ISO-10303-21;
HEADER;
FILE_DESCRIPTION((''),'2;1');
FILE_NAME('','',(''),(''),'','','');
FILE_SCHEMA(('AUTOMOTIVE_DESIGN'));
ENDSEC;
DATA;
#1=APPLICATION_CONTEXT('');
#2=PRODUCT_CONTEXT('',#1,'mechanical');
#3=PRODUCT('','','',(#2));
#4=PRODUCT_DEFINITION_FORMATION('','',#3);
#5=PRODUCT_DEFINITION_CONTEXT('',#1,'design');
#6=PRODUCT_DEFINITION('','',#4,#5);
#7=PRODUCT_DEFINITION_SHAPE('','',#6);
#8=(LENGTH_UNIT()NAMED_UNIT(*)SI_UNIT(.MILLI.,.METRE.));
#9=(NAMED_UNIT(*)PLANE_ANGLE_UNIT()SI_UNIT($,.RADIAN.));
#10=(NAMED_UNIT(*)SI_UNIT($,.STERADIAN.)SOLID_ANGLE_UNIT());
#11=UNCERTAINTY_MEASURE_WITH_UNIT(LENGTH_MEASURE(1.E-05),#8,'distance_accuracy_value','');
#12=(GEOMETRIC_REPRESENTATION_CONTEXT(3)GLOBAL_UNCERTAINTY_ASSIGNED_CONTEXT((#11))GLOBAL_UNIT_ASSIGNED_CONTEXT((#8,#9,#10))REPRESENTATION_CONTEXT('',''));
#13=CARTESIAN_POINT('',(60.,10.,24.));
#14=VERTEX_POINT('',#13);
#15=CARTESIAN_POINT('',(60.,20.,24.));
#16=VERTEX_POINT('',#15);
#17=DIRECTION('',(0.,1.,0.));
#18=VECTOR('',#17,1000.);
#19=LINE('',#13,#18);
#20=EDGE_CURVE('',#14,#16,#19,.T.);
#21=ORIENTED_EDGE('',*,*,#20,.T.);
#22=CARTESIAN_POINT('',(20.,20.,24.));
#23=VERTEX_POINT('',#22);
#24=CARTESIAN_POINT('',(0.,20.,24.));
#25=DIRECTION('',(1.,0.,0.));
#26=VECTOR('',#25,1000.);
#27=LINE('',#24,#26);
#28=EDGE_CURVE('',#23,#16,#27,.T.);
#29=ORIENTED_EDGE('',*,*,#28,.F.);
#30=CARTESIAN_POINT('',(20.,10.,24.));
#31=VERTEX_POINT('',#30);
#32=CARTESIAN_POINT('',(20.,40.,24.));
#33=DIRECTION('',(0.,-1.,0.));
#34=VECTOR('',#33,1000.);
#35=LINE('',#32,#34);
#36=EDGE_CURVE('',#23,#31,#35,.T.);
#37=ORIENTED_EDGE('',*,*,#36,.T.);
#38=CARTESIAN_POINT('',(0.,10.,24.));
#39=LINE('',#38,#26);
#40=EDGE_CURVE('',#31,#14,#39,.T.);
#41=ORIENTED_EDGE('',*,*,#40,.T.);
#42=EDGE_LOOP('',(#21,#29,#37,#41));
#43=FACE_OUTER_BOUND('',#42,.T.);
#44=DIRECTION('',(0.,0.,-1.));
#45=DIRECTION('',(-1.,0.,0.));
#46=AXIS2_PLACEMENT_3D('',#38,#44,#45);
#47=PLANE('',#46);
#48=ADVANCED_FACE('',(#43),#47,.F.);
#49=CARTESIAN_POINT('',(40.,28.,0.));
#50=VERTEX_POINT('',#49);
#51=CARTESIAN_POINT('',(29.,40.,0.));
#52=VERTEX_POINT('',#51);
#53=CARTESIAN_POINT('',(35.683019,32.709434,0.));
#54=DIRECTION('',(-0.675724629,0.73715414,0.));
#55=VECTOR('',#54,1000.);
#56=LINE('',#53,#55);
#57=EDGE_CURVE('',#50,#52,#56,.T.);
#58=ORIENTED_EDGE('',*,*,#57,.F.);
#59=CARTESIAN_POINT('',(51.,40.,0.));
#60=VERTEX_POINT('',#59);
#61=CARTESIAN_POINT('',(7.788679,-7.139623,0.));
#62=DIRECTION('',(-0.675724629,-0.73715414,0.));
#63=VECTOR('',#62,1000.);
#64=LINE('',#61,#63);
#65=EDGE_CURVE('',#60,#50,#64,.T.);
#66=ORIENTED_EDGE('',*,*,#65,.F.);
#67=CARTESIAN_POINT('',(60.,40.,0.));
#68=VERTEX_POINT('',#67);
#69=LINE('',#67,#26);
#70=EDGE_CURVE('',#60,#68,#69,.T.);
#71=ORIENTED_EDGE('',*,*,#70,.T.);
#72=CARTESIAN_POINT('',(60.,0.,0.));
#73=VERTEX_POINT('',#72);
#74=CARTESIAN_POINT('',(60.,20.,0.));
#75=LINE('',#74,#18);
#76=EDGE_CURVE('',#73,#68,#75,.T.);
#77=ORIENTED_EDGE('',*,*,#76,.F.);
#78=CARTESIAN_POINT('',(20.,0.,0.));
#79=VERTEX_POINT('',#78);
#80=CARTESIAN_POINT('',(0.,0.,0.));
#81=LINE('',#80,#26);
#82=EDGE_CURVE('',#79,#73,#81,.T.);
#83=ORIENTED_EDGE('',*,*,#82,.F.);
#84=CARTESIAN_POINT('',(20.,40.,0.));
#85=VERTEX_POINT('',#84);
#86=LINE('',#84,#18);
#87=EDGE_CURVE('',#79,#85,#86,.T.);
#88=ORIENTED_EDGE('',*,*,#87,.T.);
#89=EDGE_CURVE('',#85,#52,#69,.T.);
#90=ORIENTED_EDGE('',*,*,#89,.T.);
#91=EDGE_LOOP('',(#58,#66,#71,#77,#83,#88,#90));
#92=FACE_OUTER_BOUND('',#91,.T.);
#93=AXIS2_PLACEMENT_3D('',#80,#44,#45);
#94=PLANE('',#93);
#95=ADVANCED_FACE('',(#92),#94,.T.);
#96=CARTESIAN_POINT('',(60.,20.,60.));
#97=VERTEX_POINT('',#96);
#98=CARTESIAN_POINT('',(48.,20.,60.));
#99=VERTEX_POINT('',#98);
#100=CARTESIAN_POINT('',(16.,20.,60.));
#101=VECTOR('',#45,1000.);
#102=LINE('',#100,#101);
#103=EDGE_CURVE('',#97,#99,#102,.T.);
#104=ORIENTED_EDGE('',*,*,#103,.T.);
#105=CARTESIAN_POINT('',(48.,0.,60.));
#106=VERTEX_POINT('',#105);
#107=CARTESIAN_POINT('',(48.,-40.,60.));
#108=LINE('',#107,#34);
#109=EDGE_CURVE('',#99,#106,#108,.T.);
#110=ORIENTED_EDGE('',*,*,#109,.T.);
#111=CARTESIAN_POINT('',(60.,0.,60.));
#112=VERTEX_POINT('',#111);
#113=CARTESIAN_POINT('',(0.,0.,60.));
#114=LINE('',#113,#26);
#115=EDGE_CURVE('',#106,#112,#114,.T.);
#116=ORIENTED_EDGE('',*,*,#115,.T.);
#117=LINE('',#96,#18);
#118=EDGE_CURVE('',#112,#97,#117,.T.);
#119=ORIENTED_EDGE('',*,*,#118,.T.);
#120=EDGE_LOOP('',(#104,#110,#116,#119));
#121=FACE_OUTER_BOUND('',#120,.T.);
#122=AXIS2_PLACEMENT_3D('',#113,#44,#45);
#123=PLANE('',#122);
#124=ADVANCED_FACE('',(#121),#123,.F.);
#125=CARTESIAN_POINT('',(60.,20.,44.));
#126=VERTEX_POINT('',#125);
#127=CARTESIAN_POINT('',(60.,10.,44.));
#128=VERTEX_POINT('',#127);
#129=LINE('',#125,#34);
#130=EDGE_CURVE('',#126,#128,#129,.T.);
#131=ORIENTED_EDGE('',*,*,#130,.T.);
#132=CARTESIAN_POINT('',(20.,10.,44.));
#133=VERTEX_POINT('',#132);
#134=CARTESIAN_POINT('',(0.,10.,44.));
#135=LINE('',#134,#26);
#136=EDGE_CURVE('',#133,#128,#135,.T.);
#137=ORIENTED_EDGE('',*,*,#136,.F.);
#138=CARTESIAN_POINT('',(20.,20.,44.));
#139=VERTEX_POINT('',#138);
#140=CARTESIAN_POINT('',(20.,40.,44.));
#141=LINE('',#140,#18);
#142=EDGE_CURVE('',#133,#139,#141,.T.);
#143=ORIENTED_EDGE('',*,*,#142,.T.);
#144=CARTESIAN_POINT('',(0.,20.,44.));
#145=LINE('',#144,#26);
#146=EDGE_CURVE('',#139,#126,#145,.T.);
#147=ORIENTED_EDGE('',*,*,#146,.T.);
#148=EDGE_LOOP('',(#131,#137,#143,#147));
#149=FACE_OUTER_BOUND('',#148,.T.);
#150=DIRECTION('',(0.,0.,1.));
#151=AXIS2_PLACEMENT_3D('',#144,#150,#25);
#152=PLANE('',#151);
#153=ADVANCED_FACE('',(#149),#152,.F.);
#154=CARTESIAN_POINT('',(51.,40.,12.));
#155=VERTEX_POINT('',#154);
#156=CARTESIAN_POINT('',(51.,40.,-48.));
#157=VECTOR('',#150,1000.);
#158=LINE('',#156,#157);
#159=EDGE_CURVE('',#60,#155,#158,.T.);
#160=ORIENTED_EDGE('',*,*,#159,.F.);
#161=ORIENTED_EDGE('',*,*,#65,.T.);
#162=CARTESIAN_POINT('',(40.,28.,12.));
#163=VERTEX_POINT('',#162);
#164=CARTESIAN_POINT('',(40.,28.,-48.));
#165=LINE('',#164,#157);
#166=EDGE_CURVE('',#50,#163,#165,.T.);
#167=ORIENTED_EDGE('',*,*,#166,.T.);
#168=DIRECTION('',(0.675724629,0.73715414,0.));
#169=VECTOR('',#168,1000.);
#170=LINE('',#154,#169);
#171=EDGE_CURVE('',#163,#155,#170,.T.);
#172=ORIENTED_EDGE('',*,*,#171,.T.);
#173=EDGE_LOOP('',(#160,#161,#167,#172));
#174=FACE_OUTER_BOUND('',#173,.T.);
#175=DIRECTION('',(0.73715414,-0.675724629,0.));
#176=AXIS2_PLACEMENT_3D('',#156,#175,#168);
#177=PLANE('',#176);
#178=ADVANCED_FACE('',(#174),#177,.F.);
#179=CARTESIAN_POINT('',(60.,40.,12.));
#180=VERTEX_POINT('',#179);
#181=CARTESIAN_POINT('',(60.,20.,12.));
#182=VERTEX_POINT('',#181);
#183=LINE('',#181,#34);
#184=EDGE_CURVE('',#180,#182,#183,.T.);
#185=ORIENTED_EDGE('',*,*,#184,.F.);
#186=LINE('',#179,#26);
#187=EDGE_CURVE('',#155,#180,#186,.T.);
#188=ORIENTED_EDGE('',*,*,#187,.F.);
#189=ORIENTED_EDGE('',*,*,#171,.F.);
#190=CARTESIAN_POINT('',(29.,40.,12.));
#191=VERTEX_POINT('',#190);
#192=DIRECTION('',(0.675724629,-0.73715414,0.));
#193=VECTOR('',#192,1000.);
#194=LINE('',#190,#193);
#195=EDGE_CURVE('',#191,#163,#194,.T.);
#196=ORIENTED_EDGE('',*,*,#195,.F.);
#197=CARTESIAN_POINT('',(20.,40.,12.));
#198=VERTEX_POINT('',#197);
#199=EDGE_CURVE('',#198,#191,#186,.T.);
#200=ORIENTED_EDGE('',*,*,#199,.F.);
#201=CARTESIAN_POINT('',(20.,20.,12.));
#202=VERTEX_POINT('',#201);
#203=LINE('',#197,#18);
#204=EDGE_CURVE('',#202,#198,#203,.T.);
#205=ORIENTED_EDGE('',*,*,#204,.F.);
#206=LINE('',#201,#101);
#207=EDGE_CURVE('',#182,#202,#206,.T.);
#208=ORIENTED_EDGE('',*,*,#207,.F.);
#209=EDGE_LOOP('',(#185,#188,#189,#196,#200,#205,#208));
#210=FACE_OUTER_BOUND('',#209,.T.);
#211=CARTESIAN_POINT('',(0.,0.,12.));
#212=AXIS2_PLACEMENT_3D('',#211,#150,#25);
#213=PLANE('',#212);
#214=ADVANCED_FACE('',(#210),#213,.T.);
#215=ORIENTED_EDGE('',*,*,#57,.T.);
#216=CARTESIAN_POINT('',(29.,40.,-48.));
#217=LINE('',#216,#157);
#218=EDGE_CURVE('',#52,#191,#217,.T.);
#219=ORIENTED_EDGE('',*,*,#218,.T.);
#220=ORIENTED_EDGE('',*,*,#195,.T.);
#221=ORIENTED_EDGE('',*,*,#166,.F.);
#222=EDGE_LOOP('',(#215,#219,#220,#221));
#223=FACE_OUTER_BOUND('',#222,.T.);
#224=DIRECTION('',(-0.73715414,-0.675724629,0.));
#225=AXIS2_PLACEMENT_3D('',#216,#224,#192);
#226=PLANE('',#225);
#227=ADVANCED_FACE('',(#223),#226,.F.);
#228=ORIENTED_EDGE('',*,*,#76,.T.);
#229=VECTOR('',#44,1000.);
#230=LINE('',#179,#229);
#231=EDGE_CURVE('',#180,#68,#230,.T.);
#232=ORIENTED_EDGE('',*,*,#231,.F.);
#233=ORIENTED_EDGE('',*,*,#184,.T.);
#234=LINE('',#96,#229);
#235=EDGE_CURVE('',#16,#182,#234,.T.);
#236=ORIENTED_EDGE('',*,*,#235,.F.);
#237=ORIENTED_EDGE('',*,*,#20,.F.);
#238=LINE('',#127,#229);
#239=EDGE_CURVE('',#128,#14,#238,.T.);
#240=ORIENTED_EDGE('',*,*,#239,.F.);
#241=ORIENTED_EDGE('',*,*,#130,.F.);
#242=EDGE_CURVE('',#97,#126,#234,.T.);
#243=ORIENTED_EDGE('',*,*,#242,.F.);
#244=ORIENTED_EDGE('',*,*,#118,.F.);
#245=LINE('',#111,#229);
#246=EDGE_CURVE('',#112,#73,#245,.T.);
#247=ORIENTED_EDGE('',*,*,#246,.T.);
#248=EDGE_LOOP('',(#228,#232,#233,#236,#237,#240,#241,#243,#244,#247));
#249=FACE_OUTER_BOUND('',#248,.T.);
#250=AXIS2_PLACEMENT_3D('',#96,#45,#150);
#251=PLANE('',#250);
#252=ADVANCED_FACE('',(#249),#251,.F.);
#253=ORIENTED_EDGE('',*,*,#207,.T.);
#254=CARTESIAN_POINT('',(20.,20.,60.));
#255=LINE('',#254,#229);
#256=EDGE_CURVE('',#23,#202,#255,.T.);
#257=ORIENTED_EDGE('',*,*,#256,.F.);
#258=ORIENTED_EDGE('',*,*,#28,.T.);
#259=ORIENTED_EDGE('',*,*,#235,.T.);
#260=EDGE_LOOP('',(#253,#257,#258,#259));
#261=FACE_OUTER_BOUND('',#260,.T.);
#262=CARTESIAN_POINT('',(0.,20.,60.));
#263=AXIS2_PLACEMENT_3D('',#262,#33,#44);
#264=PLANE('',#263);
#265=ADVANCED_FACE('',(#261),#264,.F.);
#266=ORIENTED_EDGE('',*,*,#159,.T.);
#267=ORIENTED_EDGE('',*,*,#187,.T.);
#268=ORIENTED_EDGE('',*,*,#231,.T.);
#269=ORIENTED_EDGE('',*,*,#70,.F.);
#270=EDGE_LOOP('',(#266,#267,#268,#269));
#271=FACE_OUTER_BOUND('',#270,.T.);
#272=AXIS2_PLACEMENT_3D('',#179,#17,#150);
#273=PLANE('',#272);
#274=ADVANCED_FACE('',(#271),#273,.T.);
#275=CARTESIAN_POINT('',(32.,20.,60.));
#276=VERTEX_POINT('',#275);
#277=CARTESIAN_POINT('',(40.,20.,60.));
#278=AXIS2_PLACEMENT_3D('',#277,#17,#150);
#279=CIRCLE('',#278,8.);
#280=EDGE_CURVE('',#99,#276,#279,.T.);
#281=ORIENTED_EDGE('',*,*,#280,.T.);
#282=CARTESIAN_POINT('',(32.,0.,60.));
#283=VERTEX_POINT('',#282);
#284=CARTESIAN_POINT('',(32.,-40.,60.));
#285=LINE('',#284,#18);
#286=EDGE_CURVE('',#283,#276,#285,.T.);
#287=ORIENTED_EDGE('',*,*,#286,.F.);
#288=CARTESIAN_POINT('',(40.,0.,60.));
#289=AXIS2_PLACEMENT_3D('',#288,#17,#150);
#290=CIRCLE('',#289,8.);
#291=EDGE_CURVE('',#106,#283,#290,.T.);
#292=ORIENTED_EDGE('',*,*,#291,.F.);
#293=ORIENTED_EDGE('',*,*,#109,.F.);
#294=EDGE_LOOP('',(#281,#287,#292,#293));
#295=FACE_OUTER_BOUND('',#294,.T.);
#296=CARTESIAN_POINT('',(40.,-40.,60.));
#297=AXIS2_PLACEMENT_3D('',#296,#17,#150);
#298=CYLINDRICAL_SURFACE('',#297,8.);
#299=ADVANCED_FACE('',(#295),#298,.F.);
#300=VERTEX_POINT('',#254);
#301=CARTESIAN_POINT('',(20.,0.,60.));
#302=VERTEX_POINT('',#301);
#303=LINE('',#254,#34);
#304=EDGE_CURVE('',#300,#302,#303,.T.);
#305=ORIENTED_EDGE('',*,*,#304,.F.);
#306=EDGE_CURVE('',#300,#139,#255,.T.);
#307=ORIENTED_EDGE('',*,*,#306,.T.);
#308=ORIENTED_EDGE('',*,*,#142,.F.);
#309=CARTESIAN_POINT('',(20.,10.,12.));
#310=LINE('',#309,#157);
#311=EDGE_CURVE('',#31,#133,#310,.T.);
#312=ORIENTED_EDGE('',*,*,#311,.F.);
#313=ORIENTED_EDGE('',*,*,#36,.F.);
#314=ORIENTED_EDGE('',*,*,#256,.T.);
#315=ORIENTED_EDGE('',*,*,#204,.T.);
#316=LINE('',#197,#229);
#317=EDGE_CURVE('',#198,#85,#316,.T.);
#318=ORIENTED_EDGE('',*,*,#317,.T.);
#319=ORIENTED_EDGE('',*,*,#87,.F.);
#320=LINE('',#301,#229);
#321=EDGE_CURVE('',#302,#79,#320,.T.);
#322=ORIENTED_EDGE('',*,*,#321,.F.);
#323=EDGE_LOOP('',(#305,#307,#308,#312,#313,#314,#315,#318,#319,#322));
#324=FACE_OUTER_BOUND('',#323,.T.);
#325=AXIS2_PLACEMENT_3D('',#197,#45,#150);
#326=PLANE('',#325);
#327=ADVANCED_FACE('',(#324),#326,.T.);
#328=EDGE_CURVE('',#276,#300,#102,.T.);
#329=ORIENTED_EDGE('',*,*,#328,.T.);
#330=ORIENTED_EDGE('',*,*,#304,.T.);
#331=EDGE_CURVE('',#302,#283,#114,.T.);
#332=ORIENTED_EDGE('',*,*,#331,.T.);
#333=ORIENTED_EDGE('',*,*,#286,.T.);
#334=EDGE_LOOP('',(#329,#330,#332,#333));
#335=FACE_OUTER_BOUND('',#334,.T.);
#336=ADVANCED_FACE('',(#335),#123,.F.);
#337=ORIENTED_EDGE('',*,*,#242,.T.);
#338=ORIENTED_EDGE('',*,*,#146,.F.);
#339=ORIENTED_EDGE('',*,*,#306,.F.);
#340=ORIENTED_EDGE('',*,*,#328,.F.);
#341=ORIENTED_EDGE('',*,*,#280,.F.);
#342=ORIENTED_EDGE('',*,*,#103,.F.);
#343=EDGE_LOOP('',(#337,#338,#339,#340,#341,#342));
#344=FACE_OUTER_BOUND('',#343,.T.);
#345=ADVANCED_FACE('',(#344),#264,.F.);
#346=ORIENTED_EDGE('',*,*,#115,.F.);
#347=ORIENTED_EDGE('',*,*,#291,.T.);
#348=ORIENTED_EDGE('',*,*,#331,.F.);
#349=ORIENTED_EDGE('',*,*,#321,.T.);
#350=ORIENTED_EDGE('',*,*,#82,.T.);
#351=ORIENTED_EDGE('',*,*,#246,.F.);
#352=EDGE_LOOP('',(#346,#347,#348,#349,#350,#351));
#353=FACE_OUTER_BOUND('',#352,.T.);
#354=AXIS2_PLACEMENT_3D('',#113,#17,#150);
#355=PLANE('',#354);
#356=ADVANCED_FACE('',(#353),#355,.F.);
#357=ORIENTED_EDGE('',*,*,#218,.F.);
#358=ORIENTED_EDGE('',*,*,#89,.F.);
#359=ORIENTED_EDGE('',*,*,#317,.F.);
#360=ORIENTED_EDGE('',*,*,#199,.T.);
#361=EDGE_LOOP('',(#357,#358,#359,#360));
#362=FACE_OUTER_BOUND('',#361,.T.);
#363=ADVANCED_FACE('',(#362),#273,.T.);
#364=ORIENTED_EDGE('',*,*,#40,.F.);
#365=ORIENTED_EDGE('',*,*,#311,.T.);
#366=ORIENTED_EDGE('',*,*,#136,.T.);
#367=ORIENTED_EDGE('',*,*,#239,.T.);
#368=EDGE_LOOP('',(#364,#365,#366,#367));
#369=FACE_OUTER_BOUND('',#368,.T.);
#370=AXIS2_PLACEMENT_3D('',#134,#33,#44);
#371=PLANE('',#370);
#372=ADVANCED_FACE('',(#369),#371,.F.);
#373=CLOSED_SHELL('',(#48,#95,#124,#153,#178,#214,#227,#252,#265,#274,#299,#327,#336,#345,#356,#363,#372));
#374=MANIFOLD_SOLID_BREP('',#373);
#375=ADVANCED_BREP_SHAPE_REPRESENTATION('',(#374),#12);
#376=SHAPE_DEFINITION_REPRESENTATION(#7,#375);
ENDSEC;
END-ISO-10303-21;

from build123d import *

# Parameters (mm, degrees)
BASE_BODY_DEPTH        = 60
UPRIGHT_PROFILE_W      = 40
UPRIGHT_PROFILE_H      = 20
UPRIGHT_BLOCK_DEPTH    = 12
STEP_CUT_PROFILE_W     = 20
STEP_CUT_PROFILE_H     = 20
STEP_CUT_DEPTH         = 60
HALF_ROUND_NOTCH_DEPTH = 60
CROSS_SLOT_PROFILE_W   = 20
CROSS_SLOT_PROFILE_H   = 10
CROSS_SLOT_DEPTH       = 60
ANGLED_NOTCH_DEPTH     = 60


with BuildPart() as part:
    # Base Profile → Base Body (new body)
    with BuildSketch(Plane.XY):
        Polygon((0, 0), (60, 0), (60, 20), (16, 20), (0, 20), align=None)
    extrude(amount=BASE_BODY_DEPTH)

    # Upright Profile → Upright Block (add)
    with BuildSketch(Plane(origin=(0, 0, 0), x_dir=(-1, 0, 0), z_dir=(0, 0, -1))):
        with Locations((-40, 30)):
            Rectangle(UPRIGHT_PROFILE_W, UPRIGHT_PROFILE_H)
    extrude(amount=-UPRIGHT_BLOCK_DEPTH)

    # Step Cut Profile → Step Cut (cut)
    with BuildSketch(Plane(origin=(0, 0, 0), x_dir=(-1, 0, 0), z_dir=(0, 0, -1))):
        with Locations((-10, 10)):
            Rectangle(STEP_CUT_PROFILE_W, STEP_CUT_PROFILE_H)
    extrude(amount=-STEP_CUT_DEPTH, mode=Mode.SUBTRACT)

    # Half-Round Notch Profile → Half-Round Notch (cut)
    with BuildSketch(Plane(origin=(0, 20, 0), x_dir=(1, 0, 0), z_dir=(0, 1, 0))):
        with BuildLine():
            Line((32, -60), (48, -60))
            ThreePointArc((48, -60), (40, -52), (32, -60))
        make_face()
    extrude(amount=-HALF_ROUND_NOTCH_DEPTH, mode=Mode.SUBTRACT)

    # Cross Slot Profile → Cross Slot (cut)
    with BuildSketch(Plane(origin=(60, 0, 0), x_dir=(0, 0, -1), z_dir=(1, 0, 0))):
        with Locations((-34, 15)):
            Rectangle(CROSS_SLOT_PROFILE_W, CROSS_SLOT_PROFILE_H)
    extrude(amount=-CROSS_SLOT_DEPTH, mode=Mode.SUBTRACT)

    # Angled Notch Profile → Angled Notch (cut)
    with BuildSketch(Plane.XY.offset(12)):
        Polygon((40, 40), (51, 40), (40, 28), (29, 40), align=None)
    extrude(amount=-ANGLED_NOTCH_DEPTH, mode=Mode.SUBTRACT)


solid = part.part
